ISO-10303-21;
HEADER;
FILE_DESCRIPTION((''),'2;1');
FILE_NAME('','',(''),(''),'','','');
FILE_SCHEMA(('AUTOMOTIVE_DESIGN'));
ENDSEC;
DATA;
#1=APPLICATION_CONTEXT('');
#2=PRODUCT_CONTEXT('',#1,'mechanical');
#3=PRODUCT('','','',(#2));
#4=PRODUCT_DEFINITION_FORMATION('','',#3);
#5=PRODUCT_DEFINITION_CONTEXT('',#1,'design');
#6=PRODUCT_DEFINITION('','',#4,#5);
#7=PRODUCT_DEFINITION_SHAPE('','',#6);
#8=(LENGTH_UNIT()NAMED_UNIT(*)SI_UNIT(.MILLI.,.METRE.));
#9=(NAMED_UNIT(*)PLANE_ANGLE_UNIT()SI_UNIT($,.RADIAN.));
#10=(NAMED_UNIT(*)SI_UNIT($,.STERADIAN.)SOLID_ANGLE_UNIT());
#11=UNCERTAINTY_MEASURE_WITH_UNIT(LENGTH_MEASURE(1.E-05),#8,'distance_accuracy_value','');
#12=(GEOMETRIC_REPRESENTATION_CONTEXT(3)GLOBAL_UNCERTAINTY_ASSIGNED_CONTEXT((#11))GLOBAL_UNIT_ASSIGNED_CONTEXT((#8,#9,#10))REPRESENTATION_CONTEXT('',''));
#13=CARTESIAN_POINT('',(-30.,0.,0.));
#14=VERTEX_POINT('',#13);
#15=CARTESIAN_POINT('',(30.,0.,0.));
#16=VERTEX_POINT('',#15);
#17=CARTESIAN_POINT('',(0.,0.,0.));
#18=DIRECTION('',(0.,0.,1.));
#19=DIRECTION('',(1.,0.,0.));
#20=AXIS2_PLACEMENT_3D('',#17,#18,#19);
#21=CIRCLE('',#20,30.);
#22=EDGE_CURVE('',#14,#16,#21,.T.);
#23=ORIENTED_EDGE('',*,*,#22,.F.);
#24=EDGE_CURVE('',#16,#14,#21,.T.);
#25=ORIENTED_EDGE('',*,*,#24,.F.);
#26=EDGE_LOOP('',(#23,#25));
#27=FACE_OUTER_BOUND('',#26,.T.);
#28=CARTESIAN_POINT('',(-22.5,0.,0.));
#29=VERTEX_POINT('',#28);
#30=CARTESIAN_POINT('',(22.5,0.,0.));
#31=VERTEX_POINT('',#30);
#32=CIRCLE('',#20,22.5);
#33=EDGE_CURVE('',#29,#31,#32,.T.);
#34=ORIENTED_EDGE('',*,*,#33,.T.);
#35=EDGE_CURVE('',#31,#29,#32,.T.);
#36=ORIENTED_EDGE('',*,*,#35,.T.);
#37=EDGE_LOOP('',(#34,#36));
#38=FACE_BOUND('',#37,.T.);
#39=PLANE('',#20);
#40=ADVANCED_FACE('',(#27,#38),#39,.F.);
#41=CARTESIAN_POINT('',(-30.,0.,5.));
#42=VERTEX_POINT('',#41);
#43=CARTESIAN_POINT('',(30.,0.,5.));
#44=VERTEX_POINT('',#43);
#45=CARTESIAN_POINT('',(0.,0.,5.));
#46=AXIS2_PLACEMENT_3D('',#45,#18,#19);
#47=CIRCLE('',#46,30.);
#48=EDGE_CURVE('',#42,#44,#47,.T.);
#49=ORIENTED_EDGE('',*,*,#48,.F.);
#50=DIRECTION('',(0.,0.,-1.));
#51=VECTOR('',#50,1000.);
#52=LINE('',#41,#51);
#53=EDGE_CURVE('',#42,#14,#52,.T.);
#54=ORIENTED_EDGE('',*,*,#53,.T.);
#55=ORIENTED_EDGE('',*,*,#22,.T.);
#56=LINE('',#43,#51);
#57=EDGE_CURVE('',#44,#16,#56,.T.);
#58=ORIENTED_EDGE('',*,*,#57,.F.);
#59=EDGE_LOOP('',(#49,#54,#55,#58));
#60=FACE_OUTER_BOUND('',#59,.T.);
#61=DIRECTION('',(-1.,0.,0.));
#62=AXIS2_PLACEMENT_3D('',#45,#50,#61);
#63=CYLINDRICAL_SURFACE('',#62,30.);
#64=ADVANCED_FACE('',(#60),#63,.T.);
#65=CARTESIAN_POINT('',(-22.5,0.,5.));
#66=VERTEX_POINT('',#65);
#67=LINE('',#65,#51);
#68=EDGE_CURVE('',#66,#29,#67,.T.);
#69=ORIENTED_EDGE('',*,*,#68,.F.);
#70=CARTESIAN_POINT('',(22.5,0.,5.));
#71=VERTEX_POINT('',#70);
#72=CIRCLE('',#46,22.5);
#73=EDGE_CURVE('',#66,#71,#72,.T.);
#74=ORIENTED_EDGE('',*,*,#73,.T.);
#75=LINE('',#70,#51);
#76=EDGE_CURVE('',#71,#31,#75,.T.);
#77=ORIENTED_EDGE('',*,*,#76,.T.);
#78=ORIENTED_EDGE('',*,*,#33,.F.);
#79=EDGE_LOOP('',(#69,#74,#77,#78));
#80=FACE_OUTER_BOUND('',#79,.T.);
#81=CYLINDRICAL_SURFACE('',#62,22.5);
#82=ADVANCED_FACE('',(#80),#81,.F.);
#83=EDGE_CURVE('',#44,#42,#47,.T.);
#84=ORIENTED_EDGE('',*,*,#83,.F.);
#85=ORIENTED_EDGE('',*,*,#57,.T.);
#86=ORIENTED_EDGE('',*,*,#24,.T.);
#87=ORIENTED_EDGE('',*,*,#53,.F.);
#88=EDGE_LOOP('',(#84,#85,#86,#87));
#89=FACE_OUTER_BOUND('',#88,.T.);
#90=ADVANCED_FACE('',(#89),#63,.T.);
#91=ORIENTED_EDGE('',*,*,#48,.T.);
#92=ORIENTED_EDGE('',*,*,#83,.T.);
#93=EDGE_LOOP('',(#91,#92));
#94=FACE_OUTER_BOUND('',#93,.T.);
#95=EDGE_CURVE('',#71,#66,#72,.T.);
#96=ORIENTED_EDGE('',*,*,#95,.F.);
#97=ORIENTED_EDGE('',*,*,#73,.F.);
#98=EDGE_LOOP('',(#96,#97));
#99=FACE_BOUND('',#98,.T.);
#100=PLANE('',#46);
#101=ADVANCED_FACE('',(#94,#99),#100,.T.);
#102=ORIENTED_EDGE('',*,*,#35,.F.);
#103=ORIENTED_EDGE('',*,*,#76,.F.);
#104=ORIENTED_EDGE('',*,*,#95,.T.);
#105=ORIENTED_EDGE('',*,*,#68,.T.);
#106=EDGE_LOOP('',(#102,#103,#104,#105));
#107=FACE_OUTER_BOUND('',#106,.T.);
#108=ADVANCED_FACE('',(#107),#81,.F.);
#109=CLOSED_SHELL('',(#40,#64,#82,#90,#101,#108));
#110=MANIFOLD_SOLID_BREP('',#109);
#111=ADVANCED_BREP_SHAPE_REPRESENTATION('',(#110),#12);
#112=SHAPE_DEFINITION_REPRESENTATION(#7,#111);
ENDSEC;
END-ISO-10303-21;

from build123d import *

# Parameters (mm, degrees)
SKETCH1_R           = 30
SKETCH1_R_2         = 22.5
BOSS_EXTRUDE1_DEPTH = 5


with BuildPart() as part:
    # Sketch1 → Boss-Extrude1 (new body)
    with BuildSketch(Plane.XY):
        Circle(SKETCH1_R)
        Circle(SKETCH1_R_2, mode=Mode.SUBTRACT)
    extrude(amount=BOSS_EXTRUDE1_DEPTH)


solid = part.part
